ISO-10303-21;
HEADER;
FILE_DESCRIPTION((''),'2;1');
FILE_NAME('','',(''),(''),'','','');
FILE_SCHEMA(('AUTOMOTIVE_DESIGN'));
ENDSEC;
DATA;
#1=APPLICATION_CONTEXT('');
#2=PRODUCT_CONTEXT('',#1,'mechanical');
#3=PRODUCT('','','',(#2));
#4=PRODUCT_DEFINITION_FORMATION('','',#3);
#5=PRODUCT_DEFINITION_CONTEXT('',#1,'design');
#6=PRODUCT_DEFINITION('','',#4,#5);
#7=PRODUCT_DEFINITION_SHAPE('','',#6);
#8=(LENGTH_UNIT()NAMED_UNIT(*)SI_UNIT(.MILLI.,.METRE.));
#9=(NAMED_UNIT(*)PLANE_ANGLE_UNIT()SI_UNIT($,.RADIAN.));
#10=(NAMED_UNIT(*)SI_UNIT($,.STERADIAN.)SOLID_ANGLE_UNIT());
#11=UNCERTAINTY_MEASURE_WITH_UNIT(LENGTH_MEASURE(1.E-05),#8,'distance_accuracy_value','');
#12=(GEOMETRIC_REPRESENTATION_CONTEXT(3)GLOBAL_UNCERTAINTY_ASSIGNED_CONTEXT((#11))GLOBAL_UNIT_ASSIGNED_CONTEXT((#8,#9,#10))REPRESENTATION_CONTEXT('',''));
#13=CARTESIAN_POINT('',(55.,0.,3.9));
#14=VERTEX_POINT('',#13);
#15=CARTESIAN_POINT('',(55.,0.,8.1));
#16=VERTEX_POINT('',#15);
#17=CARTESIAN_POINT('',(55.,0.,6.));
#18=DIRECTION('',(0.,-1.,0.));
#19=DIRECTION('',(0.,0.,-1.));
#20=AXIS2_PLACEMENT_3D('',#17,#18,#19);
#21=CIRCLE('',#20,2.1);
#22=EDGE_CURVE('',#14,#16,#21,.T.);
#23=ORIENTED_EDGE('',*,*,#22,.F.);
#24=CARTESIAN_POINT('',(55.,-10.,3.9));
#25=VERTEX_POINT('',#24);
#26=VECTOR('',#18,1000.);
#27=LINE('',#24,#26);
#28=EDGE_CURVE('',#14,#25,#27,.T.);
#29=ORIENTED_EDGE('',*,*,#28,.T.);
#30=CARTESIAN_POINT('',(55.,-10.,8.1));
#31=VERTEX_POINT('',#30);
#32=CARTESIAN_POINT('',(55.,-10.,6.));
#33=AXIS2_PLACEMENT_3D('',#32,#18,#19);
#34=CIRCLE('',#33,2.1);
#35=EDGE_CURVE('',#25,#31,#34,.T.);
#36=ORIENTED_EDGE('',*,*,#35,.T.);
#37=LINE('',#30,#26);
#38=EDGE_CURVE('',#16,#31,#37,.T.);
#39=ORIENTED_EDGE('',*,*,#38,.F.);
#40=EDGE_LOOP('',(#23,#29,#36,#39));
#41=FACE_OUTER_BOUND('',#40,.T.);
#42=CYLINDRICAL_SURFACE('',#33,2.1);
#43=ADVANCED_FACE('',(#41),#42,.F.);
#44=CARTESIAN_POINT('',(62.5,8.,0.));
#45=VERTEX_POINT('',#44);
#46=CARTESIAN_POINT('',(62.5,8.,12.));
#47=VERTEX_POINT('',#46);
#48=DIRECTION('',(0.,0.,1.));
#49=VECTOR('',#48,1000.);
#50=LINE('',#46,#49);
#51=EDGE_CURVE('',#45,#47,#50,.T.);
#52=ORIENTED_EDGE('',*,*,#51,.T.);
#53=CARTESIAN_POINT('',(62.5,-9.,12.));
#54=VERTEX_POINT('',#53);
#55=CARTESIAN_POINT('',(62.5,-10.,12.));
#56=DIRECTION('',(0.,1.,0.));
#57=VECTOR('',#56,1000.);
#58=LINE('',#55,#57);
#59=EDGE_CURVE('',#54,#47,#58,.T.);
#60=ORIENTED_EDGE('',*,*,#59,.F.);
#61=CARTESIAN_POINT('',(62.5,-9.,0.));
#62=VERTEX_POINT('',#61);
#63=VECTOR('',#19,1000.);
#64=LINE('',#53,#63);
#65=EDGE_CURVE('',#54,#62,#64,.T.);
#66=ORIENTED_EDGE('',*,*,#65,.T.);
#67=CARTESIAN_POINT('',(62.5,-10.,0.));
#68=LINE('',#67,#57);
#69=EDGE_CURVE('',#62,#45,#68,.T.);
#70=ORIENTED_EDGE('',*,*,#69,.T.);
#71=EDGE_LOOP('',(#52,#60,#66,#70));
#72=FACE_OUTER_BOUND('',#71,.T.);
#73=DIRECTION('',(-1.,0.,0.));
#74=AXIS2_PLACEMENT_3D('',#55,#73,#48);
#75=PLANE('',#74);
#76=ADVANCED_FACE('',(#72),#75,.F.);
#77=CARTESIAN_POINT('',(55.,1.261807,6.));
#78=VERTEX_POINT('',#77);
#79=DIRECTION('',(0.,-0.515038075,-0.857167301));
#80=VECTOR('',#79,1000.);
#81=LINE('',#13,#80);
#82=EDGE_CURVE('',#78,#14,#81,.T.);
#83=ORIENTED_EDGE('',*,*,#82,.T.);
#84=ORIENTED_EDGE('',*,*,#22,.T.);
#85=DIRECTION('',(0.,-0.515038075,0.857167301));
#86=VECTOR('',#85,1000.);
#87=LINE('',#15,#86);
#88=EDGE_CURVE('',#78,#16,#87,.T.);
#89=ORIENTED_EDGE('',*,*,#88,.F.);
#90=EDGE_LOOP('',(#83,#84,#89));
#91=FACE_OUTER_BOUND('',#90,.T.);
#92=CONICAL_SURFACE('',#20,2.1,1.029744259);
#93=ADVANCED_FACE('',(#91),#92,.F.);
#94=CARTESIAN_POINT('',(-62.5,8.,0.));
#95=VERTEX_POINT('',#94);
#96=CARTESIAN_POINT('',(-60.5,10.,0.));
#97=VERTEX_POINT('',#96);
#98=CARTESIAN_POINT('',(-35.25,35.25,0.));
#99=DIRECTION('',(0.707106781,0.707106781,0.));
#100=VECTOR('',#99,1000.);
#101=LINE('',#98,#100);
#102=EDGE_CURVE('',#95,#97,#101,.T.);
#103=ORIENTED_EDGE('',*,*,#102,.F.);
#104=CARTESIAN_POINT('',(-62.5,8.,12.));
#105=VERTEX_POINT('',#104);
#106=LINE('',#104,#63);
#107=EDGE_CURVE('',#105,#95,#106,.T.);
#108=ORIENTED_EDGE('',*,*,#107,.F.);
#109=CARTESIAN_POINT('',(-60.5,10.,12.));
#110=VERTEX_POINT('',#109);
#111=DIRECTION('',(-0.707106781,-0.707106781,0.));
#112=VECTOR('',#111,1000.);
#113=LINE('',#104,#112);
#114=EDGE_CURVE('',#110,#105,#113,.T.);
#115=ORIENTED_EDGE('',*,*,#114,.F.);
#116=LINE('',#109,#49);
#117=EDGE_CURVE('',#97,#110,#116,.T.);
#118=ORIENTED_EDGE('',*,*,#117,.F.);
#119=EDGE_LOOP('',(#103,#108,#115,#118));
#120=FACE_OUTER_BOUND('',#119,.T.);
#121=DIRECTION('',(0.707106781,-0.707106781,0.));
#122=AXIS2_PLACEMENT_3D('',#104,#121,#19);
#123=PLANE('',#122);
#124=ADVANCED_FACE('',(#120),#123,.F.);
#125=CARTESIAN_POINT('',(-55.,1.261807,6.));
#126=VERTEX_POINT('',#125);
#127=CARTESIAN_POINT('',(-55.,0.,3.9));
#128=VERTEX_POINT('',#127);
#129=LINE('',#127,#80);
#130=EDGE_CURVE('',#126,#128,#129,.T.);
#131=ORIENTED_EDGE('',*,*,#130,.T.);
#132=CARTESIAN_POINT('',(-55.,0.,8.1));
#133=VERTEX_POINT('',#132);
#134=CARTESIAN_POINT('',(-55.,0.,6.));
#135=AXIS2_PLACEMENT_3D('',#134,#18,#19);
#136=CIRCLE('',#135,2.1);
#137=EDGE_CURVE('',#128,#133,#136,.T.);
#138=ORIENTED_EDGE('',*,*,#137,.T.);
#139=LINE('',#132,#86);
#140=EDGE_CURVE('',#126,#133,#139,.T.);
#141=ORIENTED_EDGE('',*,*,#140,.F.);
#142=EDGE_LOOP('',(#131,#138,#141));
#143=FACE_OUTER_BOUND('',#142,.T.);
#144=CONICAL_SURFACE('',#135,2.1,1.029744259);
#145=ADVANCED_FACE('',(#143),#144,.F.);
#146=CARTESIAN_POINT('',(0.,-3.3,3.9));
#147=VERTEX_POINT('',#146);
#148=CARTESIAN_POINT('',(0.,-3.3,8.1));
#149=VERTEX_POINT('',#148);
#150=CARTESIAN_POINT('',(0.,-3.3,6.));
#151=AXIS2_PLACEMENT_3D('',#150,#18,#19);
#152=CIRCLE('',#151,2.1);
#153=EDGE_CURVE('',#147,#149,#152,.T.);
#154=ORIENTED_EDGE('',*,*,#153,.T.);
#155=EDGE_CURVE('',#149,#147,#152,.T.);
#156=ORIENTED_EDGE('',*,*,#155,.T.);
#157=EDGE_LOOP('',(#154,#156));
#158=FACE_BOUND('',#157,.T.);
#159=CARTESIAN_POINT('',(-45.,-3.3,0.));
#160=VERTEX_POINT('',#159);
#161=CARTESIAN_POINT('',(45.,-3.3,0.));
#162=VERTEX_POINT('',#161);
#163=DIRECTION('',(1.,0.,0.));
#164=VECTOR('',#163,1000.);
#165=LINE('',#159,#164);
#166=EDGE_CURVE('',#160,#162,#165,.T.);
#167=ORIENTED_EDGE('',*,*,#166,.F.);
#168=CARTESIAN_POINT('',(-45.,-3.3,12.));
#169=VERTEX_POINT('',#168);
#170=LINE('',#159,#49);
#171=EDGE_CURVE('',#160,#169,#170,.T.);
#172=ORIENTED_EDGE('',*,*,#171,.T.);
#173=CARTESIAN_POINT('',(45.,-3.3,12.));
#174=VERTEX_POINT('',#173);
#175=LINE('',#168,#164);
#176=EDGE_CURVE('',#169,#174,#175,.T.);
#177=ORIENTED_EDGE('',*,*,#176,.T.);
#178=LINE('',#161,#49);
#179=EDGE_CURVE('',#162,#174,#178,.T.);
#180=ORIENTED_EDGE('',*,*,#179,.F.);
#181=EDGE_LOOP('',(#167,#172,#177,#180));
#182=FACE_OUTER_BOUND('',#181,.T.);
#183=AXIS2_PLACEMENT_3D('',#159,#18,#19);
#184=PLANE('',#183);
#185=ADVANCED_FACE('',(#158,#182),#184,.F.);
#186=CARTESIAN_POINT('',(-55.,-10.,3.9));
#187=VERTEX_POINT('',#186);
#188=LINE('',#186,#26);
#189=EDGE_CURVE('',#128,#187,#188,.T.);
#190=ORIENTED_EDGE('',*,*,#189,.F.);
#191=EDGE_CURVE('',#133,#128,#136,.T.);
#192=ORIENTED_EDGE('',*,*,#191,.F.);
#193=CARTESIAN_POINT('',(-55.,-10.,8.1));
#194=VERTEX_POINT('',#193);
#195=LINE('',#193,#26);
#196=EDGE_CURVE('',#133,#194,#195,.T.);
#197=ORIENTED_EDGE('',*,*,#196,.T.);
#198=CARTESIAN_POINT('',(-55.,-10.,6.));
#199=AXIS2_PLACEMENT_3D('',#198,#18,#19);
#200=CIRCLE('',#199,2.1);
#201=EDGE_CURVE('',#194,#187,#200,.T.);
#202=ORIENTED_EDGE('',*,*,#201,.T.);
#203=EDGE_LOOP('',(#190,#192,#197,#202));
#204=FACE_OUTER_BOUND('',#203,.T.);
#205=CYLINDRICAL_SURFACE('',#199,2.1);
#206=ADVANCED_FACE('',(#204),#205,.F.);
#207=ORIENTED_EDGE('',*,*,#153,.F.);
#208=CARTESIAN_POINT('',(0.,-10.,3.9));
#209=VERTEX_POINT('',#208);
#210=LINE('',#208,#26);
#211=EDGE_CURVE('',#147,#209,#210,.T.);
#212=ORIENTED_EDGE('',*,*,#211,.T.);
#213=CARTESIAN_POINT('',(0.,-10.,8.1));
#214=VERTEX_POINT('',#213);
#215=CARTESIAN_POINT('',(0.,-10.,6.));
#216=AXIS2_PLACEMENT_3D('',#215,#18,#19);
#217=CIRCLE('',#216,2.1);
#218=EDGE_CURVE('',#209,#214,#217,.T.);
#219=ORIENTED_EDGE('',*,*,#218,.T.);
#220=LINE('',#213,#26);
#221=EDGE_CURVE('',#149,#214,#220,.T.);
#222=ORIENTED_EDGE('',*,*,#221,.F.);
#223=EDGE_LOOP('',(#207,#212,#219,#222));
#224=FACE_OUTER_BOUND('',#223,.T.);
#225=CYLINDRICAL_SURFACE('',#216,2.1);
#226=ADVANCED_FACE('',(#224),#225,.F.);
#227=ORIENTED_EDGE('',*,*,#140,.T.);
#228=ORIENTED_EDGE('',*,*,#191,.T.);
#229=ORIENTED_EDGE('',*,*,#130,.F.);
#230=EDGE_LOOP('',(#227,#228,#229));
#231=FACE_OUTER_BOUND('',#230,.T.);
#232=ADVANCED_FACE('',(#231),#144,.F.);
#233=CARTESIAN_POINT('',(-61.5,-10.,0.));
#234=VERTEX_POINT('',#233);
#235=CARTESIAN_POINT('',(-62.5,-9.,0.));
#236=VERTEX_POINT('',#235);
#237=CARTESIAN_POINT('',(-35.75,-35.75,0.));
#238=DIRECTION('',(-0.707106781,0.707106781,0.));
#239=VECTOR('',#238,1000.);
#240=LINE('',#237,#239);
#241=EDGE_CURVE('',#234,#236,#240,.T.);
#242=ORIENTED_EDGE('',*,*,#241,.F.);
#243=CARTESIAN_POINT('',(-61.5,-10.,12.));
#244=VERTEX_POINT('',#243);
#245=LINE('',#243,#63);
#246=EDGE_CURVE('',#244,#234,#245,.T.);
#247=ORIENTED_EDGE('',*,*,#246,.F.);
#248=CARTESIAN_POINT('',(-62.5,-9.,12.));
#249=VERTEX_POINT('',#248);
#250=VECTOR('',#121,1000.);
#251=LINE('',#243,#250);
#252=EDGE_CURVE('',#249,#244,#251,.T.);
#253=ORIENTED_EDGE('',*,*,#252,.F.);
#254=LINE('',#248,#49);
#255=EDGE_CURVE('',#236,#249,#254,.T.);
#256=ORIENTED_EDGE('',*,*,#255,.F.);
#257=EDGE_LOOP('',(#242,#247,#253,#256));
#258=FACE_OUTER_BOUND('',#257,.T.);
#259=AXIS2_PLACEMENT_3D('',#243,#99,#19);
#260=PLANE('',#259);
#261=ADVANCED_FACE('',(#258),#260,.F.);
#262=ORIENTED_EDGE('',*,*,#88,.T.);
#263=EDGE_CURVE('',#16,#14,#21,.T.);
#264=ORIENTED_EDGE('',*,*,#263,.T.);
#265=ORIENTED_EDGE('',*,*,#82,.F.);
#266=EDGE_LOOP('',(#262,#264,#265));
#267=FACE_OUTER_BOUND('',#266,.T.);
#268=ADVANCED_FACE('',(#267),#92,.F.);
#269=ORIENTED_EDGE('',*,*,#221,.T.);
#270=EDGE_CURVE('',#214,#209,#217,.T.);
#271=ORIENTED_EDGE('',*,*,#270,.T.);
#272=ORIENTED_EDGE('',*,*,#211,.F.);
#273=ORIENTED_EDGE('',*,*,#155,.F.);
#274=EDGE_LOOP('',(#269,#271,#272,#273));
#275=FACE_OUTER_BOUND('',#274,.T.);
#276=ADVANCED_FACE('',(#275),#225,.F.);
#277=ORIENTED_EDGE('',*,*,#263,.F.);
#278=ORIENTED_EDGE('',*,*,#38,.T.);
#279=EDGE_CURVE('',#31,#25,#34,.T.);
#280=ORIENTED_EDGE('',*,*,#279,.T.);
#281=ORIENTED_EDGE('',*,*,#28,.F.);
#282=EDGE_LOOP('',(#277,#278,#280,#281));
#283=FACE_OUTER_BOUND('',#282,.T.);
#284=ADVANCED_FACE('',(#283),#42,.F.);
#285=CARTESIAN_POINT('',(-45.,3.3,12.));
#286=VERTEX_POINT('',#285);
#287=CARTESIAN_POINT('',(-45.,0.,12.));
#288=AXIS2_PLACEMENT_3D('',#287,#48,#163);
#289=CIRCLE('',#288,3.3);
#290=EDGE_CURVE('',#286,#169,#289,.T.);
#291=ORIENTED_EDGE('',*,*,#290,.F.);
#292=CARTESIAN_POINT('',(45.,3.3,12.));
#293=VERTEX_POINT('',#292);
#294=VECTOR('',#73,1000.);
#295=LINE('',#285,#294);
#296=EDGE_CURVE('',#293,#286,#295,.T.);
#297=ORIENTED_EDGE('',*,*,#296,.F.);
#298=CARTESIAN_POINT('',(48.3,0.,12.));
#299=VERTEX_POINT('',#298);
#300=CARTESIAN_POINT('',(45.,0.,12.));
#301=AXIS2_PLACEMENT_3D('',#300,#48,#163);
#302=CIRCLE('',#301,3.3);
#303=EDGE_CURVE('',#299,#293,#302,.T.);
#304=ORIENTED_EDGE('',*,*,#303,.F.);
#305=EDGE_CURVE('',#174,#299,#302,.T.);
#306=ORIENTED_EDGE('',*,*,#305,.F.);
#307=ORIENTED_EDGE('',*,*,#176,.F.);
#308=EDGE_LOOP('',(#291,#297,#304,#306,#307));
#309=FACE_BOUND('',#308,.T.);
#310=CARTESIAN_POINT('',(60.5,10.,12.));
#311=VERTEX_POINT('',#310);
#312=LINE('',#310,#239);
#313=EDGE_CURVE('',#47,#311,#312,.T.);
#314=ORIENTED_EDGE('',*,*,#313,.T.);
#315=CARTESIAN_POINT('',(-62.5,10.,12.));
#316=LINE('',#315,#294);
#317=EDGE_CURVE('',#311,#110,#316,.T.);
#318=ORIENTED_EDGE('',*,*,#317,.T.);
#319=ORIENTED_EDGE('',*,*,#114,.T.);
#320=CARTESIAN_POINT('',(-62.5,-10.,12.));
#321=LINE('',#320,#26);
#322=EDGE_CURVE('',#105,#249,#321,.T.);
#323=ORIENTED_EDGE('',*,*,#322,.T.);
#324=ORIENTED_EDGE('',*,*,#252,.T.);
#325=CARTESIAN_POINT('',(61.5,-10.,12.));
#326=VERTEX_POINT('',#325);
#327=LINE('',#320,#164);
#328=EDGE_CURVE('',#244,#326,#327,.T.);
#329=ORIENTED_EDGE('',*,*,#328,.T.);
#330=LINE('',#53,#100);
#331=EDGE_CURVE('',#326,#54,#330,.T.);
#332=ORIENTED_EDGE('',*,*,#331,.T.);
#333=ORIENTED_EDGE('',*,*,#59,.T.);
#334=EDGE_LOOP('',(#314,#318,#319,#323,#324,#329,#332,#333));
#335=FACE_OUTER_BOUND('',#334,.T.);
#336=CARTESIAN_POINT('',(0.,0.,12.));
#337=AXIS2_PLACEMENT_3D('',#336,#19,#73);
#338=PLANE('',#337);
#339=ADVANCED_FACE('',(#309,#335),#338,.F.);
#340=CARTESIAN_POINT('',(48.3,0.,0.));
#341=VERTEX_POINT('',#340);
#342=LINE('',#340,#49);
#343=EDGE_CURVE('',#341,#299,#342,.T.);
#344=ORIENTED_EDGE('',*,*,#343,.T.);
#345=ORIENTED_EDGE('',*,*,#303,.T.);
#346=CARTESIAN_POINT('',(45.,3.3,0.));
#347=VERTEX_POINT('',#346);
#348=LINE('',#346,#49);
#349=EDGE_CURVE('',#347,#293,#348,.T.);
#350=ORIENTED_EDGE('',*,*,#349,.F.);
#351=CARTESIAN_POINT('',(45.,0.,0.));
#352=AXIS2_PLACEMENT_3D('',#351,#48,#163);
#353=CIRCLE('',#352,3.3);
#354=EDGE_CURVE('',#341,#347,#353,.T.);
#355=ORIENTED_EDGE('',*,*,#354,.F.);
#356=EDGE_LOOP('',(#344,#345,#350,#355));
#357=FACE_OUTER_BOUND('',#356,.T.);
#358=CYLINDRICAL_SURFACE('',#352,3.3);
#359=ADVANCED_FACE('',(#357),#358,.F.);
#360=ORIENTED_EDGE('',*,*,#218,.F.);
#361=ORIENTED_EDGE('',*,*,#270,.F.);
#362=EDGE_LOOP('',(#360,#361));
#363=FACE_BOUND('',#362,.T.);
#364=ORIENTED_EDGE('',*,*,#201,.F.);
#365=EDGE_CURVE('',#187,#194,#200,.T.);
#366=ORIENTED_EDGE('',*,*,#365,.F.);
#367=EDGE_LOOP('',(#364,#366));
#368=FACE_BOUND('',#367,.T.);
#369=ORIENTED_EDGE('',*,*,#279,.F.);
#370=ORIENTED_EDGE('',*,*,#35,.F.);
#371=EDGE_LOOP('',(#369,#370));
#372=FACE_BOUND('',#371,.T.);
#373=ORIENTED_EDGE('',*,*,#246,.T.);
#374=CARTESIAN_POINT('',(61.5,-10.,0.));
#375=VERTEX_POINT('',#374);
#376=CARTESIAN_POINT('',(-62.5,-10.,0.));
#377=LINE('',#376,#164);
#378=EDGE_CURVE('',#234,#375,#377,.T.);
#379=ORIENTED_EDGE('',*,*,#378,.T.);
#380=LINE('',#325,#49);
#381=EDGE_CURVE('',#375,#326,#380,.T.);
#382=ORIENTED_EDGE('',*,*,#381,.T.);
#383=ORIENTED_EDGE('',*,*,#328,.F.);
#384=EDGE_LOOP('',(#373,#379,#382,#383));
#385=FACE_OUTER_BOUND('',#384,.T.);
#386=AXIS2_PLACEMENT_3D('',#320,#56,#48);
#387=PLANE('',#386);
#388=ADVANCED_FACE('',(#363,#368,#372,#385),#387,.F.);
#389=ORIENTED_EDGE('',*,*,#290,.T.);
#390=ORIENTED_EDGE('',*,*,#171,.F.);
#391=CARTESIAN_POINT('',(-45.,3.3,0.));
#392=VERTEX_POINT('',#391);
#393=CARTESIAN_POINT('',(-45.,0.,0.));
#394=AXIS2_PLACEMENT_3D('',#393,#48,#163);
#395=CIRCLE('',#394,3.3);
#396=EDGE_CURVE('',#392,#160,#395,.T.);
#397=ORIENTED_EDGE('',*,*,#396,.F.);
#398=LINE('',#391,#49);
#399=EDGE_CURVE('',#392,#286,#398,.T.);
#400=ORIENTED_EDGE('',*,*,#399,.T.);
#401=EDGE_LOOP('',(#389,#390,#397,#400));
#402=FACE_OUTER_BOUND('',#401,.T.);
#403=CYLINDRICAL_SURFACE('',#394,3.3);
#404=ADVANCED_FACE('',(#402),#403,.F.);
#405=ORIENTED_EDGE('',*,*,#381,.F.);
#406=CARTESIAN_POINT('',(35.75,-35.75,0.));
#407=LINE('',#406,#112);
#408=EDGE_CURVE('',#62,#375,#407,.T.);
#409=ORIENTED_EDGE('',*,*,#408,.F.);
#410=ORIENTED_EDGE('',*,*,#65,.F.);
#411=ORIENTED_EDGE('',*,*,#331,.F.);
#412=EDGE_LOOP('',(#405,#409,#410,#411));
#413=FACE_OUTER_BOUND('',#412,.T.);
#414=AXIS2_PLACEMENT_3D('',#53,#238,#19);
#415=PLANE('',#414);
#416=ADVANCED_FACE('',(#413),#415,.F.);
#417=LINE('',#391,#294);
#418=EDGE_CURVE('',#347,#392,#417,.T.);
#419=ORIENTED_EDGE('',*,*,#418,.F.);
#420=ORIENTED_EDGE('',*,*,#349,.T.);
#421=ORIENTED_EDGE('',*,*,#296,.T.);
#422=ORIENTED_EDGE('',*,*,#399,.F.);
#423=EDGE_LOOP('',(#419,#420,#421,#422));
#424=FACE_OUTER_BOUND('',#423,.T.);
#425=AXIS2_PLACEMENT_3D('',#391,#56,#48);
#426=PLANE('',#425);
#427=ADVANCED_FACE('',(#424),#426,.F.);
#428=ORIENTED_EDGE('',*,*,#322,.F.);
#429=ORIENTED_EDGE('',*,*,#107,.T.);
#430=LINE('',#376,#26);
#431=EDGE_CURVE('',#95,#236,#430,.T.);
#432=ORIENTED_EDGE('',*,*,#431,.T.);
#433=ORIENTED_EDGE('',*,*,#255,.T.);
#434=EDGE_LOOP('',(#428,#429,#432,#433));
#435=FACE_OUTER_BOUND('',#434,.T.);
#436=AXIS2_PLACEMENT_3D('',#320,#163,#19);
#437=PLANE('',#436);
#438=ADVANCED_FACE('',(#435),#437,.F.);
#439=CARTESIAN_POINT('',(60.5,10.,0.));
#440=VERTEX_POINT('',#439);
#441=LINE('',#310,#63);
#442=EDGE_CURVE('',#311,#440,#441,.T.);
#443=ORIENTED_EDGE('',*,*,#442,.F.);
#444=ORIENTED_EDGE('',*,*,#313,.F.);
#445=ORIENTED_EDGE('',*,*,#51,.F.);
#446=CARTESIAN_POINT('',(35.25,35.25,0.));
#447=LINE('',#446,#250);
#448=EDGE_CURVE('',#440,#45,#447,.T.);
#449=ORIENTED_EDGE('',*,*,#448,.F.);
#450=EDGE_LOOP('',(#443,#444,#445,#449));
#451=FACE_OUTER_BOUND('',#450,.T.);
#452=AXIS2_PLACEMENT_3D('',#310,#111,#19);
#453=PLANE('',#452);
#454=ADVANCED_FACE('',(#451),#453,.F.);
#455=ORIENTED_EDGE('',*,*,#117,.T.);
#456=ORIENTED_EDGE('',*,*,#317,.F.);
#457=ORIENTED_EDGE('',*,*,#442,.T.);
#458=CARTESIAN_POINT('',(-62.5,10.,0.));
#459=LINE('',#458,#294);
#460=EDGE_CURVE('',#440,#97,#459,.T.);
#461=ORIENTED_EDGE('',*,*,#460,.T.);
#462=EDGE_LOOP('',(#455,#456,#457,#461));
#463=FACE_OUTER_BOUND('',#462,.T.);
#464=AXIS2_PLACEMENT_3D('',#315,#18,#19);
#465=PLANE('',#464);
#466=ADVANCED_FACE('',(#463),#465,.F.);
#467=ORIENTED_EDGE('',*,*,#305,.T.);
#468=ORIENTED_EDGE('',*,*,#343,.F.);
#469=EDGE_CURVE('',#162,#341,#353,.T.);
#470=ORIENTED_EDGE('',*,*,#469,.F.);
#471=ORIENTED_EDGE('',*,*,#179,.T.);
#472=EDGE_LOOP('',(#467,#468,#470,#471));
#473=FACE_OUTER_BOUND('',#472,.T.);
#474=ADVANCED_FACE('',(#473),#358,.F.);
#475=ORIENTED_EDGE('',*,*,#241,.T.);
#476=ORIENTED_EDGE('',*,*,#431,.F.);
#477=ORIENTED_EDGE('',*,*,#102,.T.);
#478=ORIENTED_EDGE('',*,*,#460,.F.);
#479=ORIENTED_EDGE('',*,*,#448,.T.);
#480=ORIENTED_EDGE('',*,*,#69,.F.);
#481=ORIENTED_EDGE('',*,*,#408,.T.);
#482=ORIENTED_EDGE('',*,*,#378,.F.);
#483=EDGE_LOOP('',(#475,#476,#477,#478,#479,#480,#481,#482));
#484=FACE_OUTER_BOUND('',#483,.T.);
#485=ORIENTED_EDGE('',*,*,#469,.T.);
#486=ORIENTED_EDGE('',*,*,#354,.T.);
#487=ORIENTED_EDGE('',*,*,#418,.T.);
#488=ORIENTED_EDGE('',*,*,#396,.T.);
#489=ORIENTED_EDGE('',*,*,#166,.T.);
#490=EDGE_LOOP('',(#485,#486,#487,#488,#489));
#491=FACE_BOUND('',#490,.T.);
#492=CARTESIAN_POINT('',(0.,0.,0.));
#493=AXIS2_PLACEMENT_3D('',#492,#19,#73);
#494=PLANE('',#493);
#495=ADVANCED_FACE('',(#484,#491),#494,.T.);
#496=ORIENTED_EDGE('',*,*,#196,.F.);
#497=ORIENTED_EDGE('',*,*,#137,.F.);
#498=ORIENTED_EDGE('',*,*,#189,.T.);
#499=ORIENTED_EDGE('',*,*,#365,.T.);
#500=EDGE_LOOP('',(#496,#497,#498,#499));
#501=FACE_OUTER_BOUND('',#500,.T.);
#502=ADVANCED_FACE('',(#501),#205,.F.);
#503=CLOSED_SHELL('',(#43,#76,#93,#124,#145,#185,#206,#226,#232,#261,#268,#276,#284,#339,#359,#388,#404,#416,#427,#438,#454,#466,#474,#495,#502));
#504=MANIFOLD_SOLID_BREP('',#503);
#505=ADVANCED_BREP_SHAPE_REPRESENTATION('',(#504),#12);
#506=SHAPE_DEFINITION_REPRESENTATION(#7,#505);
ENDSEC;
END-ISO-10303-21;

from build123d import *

# Parameters (mm, degrees)
SKETCH_1_W             = 125
SKETCH_1_H             = 20
EXTRUDE_1_DEPTH        = 12
CUT_EXTRUDE_1_DEPTH    = 65.422433981
HOLE_WIZARD_M5_1_D     = 4.2
HOLE_WIZARD_M5_1_DEPTH = 10
HOLE_WIZARD_M5_1_TIP   = 1.2618073
CHAMFER_1_SIZE         = 2
CHAMFER_2_SIZE         = 1


with BuildPart() as part:
    # 草图1 → 凸台-拉伸1 (new body)
    with BuildSketch(Plane.XY):
        Rectangle(SKETCH_1_W, SKETCH_1_H)
    extrude(amount=EXTRUDE_1_DEPTH)

    # 草图2 → 切除-拉伸1 (cut, through all)
    with BuildSketch(Plane.XY.offset(12)):
        with BuildLine():
            Line((-45, 3.3), (45, 3.3))
            ThreePointArc((45, 3.3), (48.3, 0), (45, -3.3))
            Line((45, -3.3), (-45, -3.3))
            ThreePointArc((-45, -3.3), (-48.3, 0), (-45, 3.3))
        make_face()
    extrude(amount=-CUT_EXTRUDE_1_DEPTH, mode=Mode.SUBTRACT)

    # M5 螺纹孔1
    with Locations(Plane(origin=(0, -10, 0), x_dir=(-1, 0, 0), z_dir=(0, -1, 0))):
        with Locations((55, -6), (0, -6), (-55, -6)):
            Hole(HOLE_WIZARD_M5_1_D / 2, depth=HOLE_WIZARD_M5_1_DEPTH)
            with Locations((0, 0, -(HOLE_WIZARD_M5_1_DEPTH + HOLE_WIZARD_M5_1_TIP / 2))):  # 118° drill point
                Cone(0, HOLE_WIZARD_M5_1_D / 2, HOLE_WIZARD_M5_1_TIP, mode=Mode.SUBTRACT)

    # 倒角1
    chamfer_1_edges = [part.edges().sort_by_distance(p)[0] for p in [
        (-62.5, 10, 6),
        (62.5, 10, 6),
    ]]
    chamfer(chamfer_1_edges, length=CHAMFER_1_SIZE)

    # 倒角2
    chamfer_2_edges = [part.edges().sort_by_distance(p)[0] for p in [
        (62.5, -10, 6),
        (-62.5, -10, 6),
    ]]
    chamfer(chamfer_2_edges, length=CHAMFER_2_SIZE)


solid = part.part
